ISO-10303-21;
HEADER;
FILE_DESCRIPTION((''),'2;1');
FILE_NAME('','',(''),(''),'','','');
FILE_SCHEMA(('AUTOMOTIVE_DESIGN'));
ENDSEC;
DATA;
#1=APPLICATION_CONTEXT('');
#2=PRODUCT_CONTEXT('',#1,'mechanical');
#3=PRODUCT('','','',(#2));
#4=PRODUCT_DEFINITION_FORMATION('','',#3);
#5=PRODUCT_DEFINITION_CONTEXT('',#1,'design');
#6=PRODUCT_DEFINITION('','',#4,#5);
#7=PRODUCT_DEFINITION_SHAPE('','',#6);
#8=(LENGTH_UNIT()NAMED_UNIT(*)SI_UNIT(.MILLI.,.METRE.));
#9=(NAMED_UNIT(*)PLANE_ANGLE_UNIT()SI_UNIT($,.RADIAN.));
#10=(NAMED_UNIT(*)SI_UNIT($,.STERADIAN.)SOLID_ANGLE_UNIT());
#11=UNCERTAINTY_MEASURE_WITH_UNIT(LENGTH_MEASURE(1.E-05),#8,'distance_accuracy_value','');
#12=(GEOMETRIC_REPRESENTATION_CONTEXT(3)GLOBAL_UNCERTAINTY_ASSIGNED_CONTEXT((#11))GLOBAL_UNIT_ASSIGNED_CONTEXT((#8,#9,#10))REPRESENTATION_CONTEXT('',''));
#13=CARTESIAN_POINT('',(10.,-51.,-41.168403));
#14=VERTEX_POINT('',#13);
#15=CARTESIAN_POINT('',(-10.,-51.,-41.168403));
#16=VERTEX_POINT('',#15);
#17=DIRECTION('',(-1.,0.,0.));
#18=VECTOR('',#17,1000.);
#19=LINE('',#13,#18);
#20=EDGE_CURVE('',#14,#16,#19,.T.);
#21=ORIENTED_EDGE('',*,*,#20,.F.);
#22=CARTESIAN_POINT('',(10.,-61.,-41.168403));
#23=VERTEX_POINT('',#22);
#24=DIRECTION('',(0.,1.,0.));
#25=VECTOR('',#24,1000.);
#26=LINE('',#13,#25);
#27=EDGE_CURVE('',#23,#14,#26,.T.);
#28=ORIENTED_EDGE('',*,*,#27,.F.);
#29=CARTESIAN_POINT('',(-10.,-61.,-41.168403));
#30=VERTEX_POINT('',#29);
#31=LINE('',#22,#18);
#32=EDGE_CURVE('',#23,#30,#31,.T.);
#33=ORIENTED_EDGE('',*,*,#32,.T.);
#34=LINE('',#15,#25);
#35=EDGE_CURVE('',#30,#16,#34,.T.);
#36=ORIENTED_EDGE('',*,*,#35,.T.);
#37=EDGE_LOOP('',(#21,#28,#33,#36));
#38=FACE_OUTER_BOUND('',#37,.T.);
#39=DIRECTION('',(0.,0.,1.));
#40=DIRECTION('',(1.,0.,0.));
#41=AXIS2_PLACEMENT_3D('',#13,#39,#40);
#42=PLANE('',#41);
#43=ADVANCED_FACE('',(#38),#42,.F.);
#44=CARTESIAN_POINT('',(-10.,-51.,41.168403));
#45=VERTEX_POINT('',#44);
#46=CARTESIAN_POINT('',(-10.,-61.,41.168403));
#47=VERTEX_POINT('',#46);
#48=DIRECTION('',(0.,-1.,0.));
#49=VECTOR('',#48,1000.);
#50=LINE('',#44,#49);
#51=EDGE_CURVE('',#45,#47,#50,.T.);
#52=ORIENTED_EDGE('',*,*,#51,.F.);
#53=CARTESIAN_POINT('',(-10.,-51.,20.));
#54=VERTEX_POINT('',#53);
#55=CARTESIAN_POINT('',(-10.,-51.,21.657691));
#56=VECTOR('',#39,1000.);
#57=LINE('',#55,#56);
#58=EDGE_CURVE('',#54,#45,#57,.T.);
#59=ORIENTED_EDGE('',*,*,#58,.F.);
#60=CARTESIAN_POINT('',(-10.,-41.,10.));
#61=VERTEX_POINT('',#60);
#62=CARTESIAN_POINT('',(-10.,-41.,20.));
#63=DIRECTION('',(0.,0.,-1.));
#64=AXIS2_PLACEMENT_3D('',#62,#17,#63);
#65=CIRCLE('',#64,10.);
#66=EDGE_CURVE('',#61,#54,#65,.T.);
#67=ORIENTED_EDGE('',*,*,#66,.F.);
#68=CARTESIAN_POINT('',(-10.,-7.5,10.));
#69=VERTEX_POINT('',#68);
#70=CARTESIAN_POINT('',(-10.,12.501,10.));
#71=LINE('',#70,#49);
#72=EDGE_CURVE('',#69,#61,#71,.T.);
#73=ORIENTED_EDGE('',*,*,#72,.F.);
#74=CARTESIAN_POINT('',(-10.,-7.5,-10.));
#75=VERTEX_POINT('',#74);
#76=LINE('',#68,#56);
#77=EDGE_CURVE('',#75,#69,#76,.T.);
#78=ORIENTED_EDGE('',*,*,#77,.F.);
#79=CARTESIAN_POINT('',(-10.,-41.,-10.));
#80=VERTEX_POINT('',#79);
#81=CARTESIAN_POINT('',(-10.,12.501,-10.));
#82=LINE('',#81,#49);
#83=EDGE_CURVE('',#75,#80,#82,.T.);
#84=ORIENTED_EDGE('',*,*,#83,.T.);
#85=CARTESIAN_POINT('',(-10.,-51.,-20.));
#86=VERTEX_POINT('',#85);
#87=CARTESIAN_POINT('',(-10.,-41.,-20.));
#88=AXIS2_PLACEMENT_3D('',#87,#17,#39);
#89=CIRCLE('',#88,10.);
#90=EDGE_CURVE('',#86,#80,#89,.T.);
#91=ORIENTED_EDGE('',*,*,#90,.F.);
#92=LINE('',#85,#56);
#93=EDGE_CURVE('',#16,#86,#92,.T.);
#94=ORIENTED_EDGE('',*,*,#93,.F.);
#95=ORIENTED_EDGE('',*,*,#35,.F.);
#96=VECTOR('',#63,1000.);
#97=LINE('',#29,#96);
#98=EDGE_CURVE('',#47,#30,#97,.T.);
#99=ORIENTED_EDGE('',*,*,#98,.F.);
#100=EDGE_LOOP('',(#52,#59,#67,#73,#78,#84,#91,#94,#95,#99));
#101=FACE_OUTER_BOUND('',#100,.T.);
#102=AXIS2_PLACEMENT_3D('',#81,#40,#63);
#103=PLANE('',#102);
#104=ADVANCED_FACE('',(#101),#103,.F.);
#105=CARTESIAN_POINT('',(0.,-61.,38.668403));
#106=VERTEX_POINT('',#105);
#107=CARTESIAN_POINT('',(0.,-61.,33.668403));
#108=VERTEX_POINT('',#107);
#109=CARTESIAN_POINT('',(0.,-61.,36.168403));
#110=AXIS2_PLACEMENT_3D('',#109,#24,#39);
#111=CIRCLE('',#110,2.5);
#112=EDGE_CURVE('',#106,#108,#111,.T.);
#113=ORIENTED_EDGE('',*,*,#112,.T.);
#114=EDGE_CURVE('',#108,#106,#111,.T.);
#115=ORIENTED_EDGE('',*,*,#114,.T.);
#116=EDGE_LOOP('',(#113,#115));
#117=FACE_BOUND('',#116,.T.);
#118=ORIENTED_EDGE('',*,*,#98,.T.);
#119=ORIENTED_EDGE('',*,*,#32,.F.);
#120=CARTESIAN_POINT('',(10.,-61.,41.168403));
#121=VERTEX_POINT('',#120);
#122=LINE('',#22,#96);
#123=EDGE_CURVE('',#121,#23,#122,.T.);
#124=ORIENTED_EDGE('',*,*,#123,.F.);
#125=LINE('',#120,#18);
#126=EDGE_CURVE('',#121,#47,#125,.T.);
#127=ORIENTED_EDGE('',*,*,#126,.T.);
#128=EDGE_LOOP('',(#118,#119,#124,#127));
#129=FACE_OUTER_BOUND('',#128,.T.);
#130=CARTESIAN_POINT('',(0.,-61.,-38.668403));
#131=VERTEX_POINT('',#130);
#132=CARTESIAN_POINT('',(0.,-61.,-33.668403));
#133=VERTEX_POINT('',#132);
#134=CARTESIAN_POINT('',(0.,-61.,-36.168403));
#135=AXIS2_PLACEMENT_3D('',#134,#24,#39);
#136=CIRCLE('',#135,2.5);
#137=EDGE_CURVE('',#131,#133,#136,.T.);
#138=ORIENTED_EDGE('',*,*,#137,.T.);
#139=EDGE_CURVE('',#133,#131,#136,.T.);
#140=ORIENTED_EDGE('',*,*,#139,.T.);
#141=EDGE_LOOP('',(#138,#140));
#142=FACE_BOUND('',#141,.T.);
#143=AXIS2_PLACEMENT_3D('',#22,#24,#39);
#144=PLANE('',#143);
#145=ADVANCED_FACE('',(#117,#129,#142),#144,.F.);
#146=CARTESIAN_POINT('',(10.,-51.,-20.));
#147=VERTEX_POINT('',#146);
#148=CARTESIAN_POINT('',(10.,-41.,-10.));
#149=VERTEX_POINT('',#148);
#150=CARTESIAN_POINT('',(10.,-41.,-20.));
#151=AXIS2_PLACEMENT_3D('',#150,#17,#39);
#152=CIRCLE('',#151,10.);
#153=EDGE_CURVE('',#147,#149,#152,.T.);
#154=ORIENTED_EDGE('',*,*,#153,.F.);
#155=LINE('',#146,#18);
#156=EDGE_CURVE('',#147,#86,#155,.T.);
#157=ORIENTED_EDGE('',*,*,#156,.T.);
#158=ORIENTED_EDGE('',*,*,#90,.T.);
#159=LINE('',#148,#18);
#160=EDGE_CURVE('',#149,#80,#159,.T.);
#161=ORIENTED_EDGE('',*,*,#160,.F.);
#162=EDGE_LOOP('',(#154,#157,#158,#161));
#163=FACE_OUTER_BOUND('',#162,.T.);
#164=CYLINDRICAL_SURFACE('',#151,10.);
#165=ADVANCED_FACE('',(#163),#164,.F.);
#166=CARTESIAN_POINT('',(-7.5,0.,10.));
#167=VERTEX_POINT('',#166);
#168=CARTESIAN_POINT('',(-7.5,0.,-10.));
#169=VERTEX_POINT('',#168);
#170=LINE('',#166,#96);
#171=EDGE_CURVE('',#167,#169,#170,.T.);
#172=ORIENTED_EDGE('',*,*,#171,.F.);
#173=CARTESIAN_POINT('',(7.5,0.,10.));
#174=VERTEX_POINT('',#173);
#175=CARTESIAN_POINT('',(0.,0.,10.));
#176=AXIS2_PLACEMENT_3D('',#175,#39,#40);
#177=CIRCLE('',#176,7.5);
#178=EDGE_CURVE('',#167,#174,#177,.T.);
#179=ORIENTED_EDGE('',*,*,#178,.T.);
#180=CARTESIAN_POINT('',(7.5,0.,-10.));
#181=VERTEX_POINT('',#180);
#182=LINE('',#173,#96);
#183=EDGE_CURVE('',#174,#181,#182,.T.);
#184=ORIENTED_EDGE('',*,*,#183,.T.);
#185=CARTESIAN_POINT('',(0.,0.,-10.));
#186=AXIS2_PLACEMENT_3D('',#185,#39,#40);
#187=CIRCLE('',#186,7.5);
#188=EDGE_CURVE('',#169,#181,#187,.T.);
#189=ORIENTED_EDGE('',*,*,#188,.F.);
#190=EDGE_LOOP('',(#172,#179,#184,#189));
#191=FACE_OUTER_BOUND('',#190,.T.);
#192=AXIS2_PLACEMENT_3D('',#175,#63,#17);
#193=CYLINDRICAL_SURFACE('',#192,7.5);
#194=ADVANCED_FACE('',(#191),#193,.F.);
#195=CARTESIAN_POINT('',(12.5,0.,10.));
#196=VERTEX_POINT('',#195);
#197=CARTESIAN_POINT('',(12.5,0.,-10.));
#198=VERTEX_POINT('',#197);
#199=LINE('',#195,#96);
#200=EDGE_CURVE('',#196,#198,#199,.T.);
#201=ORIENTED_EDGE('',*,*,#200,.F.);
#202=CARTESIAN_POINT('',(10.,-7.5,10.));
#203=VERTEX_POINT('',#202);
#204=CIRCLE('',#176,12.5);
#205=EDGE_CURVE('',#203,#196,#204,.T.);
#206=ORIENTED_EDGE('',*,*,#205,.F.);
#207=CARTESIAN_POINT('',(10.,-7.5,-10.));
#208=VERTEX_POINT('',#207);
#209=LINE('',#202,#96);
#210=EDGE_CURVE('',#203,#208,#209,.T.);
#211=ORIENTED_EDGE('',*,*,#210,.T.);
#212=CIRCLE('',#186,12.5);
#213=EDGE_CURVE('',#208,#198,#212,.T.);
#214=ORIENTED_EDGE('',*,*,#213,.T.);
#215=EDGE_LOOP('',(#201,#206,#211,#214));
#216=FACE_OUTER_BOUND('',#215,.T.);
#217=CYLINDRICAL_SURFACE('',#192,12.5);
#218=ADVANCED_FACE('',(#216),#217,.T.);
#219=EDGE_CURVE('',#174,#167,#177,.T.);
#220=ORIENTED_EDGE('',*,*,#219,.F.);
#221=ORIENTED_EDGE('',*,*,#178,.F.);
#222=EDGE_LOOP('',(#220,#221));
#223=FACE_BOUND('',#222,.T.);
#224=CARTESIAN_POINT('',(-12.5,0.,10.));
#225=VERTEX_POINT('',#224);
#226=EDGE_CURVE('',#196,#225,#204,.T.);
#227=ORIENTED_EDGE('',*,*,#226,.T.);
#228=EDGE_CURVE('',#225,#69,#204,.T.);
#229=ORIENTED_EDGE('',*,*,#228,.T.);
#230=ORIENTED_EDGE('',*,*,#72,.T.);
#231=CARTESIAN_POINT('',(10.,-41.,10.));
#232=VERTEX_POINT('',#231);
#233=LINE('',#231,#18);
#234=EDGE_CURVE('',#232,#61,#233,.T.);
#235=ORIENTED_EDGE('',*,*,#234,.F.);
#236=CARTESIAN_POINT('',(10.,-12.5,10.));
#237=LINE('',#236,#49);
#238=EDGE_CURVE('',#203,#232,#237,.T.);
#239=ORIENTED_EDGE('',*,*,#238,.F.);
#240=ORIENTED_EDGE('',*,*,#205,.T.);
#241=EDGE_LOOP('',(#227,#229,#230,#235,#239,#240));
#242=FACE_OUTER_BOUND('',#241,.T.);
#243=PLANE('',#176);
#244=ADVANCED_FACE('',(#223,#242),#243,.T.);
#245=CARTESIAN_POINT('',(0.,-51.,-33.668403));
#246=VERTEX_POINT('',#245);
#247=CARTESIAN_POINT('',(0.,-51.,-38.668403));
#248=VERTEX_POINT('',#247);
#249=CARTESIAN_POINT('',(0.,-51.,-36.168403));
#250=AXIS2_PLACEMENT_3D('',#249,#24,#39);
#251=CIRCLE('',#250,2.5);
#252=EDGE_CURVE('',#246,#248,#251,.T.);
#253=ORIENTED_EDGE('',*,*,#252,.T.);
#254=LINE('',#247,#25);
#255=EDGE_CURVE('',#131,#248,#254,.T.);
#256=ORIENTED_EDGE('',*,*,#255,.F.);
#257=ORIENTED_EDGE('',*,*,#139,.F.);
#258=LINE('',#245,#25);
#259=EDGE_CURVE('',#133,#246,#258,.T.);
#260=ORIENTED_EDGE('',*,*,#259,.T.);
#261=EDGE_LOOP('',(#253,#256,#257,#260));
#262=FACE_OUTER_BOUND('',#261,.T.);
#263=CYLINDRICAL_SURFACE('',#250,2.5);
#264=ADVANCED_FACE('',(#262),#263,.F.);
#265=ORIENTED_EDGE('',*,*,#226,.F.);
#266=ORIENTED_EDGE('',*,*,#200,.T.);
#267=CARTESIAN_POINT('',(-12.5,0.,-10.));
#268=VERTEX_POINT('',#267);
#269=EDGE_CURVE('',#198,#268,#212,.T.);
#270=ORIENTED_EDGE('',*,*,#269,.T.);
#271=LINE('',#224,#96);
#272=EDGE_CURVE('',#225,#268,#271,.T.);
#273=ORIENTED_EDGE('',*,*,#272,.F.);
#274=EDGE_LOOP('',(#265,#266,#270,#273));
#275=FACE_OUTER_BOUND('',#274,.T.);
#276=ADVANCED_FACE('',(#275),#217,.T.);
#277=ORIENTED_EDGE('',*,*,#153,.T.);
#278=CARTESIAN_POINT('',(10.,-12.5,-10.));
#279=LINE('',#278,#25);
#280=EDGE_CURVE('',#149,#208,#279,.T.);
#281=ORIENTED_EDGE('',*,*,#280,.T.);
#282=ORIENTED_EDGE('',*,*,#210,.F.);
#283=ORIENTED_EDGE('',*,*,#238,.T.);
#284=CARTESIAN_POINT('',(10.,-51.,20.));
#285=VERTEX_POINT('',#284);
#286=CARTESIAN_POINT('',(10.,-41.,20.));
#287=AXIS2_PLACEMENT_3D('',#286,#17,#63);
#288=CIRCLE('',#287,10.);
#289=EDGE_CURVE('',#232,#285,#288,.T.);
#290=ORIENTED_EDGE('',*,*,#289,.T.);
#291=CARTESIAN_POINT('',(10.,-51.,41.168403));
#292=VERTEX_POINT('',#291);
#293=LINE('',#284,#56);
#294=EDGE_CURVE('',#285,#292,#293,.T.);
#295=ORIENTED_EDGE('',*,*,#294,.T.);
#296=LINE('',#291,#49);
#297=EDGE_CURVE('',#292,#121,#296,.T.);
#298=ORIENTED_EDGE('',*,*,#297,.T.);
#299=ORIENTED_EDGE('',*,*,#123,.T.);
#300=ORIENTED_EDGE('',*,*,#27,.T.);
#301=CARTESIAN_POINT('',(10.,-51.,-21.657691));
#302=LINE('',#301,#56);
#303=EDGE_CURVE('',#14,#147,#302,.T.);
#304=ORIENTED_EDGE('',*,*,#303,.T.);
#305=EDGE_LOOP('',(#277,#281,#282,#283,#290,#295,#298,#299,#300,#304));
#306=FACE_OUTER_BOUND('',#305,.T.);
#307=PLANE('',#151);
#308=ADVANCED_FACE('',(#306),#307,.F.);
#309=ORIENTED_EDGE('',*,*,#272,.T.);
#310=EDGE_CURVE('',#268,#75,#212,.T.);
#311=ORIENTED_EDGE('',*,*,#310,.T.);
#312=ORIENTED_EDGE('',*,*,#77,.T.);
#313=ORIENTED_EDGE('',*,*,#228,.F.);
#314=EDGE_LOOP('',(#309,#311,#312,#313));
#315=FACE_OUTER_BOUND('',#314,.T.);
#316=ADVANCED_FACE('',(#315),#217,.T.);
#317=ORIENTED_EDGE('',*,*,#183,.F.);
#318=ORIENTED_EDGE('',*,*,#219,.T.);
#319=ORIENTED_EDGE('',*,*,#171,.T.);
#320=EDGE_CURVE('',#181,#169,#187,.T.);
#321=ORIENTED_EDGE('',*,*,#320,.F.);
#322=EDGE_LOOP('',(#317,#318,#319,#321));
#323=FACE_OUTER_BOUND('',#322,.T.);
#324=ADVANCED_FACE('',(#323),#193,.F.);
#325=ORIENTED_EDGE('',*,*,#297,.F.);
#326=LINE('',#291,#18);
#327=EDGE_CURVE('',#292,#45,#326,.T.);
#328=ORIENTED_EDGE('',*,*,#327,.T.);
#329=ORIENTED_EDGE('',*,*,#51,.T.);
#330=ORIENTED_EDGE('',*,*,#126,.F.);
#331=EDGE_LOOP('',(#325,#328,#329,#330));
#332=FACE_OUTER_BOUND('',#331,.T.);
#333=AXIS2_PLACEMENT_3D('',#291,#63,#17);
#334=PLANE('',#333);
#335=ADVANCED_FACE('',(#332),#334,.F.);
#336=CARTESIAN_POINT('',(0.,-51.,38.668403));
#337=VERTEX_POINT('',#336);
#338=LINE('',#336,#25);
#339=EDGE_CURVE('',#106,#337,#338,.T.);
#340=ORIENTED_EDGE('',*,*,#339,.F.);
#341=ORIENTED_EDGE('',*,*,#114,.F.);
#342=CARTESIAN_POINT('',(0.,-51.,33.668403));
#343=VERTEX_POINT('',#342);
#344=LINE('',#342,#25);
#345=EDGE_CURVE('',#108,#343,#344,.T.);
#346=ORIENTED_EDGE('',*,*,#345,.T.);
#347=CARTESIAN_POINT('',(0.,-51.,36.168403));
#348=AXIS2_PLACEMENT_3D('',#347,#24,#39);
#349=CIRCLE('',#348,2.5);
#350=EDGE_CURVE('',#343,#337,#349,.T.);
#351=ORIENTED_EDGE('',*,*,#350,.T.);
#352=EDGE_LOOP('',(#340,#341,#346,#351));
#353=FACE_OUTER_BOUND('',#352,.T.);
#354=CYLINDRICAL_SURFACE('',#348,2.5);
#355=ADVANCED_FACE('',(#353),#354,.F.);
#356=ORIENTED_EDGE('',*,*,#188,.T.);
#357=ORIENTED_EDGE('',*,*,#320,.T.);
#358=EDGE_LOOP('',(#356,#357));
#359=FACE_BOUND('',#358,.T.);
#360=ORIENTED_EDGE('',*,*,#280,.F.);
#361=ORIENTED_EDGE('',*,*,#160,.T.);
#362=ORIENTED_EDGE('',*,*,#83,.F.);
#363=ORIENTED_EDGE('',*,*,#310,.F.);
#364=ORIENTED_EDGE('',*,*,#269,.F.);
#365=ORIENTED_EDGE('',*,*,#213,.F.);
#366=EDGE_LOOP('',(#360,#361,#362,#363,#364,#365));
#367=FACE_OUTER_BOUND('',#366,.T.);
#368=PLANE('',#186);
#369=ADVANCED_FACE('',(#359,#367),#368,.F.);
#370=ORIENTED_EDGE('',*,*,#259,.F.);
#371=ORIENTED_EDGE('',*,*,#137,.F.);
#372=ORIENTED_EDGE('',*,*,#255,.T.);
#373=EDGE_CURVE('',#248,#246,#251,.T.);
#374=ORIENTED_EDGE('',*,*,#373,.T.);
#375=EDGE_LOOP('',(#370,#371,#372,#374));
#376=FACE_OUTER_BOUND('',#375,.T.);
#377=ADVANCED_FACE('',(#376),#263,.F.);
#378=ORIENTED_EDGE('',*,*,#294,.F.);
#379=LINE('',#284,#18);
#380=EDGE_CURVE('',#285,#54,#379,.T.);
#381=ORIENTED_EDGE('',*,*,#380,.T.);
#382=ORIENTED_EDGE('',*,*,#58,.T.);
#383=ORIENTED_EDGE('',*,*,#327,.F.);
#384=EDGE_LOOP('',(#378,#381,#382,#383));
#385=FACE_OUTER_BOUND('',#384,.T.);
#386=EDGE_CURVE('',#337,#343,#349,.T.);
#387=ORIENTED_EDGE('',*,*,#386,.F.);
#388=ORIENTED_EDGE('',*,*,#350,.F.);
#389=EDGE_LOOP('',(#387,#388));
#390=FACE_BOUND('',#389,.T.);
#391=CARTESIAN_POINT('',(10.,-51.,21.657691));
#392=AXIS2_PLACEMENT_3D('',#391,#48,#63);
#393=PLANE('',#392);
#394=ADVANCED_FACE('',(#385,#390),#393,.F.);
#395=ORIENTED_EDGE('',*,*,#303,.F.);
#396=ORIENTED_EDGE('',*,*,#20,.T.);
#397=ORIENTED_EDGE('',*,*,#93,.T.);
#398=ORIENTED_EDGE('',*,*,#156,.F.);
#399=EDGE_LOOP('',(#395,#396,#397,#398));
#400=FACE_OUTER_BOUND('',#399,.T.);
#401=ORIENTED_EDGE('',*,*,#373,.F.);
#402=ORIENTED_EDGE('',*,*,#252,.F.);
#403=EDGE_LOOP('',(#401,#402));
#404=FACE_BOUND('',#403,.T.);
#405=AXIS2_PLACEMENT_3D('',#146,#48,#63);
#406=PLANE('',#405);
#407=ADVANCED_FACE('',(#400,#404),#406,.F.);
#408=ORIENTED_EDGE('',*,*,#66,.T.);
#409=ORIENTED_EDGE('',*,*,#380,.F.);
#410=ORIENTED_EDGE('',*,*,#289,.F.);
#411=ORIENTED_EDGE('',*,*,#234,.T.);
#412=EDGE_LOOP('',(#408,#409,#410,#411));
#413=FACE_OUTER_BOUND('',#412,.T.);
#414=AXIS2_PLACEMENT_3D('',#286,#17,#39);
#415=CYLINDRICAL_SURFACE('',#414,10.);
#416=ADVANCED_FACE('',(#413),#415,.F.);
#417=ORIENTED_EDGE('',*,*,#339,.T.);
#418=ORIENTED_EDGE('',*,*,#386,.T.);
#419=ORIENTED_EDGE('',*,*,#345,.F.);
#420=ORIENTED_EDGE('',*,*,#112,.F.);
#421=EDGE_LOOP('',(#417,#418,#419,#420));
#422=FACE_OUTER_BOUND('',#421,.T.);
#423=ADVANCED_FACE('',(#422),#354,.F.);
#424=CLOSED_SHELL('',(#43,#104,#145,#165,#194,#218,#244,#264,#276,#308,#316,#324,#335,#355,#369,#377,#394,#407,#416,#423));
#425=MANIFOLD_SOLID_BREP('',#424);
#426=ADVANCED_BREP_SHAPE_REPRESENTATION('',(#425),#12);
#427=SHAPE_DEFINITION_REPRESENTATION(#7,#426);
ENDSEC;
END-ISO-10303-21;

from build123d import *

# Parameters (mm, degrees)
SKETCH_1_R           = 12.5
SKETCH_1_R_2         = 7.5
EXTRUDE_1_DEPTH      = 10
EXTRUDE_3_DEPTH      = 10
EXTRUDE_4_REACH      = 66.833
EXTRUDE_4_END_RADIUS = 12.5
SKETCH_6_W           = 20
SKETCH_6_H           = 20
HOLE_WIZARD_M6_1_D   = 5


with BuildPart() as part:
    # 草图1 → 凸台-拉伸1 (new, symmetric)
    with BuildSketch(Plane.XY):
        Circle(SKETCH_1_R)
        Circle(SKETCH_1_R_2, mode=Mode.SUBTRACT)
    extrude(amount=EXTRUDE_1_DEPTH, both=True)



with BuildPart() as body_2:
    # 草图5 → 凸台-拉伸3 (new, symmetric)
    with BuildSketch(Plane(origin=(0, 0, 0), x_dir=(0, 0, -1), z_dir=(1, 0, 0))):
        with BuildLine():
            Line((21.657691454, -51), (41.168402769, -51))
            Line((41.168402769, -51), (41.168402769, -61))
            Line((41.168402769, -61), (-41.168402769, -61))
            Line((-41.168402769, -61), (-41.168402769, -51))
            Line((-41.168402769, -51), (-21.657691454, -51))
            Line((-21.657691454, -51), (-20, -51))
            ThreePointArc((-20, -51), (-12.928932188, -48.071067812), (-10, -41))
            Line((-10, -41), (-10, -12.5))
            Line((-10, -12.5), (10, -12.5))
            Line((10, -12.5), (10, -41))
            ThreePointArc((10, -41), (12.928932188, -48.071067812), (20, -51))
            Line((20, -51), (21.657691454, -51))
        make_face()
    extrude(amount=EXTRUDE_3_DEPTH, both=True)


with BuildPart() as part_1:
    add(part.part)

    add(body_2.part)  # 凸台-拉伸4 merges body 2
    # 凸台-拉伸4: up to this cylinder (the profile starts outside it)
    extrude_4_end = Plane(origin=(0, 0, 0), z_dir=(0, 0, -1)) * Cylinder(EXTRUDE_4_END_RADIUS, 159.666, mode=Mode.PRIVATE)
    # 草图6 → 凸台-拉伸4 (add, up to the surface)
    with BuildSketch(Plane(origin=(0, -12.5, 0), x_dir=(1, 0, 0), z_dir=(0, 1, 0)), mode=Mode.PRIVATE) as extrude_4_sk1:
        Rectangle(SKETCH_6_W, SKETCH_6_H)
    extrude_4_tool1 = extrude(extrude_4_sk1.sketch, amount=EXTRUDE_4_REACH, mode=Mode.PRIVATE) - extrude_4_end
    add(extrude_4_tool1.solids().sort_by_distance((0, -12.5, 0))[0])
    add(extrude_4_tool1.solids().sort_by_distance((0, -12.5, 0))[1])

    # M6 螺纹孔1 (through all)
    with Locations(Plane(origin=(0, -51, 36.168402769), x_dir=(0, 0, 1), z_dir=(0, 1, 0))):
        with Locations((0, 0)):
            hole_wizard_m6_1 = Hole(HOLE_WIZARD_M6_1_D / 2)

    # 镜向1: M6 螺纹孔1 across plane
    add(hole_wizard_m6_1.mirror(Plane.XY), mode=Mode.SUBTRACT)


solid = part_1.part
